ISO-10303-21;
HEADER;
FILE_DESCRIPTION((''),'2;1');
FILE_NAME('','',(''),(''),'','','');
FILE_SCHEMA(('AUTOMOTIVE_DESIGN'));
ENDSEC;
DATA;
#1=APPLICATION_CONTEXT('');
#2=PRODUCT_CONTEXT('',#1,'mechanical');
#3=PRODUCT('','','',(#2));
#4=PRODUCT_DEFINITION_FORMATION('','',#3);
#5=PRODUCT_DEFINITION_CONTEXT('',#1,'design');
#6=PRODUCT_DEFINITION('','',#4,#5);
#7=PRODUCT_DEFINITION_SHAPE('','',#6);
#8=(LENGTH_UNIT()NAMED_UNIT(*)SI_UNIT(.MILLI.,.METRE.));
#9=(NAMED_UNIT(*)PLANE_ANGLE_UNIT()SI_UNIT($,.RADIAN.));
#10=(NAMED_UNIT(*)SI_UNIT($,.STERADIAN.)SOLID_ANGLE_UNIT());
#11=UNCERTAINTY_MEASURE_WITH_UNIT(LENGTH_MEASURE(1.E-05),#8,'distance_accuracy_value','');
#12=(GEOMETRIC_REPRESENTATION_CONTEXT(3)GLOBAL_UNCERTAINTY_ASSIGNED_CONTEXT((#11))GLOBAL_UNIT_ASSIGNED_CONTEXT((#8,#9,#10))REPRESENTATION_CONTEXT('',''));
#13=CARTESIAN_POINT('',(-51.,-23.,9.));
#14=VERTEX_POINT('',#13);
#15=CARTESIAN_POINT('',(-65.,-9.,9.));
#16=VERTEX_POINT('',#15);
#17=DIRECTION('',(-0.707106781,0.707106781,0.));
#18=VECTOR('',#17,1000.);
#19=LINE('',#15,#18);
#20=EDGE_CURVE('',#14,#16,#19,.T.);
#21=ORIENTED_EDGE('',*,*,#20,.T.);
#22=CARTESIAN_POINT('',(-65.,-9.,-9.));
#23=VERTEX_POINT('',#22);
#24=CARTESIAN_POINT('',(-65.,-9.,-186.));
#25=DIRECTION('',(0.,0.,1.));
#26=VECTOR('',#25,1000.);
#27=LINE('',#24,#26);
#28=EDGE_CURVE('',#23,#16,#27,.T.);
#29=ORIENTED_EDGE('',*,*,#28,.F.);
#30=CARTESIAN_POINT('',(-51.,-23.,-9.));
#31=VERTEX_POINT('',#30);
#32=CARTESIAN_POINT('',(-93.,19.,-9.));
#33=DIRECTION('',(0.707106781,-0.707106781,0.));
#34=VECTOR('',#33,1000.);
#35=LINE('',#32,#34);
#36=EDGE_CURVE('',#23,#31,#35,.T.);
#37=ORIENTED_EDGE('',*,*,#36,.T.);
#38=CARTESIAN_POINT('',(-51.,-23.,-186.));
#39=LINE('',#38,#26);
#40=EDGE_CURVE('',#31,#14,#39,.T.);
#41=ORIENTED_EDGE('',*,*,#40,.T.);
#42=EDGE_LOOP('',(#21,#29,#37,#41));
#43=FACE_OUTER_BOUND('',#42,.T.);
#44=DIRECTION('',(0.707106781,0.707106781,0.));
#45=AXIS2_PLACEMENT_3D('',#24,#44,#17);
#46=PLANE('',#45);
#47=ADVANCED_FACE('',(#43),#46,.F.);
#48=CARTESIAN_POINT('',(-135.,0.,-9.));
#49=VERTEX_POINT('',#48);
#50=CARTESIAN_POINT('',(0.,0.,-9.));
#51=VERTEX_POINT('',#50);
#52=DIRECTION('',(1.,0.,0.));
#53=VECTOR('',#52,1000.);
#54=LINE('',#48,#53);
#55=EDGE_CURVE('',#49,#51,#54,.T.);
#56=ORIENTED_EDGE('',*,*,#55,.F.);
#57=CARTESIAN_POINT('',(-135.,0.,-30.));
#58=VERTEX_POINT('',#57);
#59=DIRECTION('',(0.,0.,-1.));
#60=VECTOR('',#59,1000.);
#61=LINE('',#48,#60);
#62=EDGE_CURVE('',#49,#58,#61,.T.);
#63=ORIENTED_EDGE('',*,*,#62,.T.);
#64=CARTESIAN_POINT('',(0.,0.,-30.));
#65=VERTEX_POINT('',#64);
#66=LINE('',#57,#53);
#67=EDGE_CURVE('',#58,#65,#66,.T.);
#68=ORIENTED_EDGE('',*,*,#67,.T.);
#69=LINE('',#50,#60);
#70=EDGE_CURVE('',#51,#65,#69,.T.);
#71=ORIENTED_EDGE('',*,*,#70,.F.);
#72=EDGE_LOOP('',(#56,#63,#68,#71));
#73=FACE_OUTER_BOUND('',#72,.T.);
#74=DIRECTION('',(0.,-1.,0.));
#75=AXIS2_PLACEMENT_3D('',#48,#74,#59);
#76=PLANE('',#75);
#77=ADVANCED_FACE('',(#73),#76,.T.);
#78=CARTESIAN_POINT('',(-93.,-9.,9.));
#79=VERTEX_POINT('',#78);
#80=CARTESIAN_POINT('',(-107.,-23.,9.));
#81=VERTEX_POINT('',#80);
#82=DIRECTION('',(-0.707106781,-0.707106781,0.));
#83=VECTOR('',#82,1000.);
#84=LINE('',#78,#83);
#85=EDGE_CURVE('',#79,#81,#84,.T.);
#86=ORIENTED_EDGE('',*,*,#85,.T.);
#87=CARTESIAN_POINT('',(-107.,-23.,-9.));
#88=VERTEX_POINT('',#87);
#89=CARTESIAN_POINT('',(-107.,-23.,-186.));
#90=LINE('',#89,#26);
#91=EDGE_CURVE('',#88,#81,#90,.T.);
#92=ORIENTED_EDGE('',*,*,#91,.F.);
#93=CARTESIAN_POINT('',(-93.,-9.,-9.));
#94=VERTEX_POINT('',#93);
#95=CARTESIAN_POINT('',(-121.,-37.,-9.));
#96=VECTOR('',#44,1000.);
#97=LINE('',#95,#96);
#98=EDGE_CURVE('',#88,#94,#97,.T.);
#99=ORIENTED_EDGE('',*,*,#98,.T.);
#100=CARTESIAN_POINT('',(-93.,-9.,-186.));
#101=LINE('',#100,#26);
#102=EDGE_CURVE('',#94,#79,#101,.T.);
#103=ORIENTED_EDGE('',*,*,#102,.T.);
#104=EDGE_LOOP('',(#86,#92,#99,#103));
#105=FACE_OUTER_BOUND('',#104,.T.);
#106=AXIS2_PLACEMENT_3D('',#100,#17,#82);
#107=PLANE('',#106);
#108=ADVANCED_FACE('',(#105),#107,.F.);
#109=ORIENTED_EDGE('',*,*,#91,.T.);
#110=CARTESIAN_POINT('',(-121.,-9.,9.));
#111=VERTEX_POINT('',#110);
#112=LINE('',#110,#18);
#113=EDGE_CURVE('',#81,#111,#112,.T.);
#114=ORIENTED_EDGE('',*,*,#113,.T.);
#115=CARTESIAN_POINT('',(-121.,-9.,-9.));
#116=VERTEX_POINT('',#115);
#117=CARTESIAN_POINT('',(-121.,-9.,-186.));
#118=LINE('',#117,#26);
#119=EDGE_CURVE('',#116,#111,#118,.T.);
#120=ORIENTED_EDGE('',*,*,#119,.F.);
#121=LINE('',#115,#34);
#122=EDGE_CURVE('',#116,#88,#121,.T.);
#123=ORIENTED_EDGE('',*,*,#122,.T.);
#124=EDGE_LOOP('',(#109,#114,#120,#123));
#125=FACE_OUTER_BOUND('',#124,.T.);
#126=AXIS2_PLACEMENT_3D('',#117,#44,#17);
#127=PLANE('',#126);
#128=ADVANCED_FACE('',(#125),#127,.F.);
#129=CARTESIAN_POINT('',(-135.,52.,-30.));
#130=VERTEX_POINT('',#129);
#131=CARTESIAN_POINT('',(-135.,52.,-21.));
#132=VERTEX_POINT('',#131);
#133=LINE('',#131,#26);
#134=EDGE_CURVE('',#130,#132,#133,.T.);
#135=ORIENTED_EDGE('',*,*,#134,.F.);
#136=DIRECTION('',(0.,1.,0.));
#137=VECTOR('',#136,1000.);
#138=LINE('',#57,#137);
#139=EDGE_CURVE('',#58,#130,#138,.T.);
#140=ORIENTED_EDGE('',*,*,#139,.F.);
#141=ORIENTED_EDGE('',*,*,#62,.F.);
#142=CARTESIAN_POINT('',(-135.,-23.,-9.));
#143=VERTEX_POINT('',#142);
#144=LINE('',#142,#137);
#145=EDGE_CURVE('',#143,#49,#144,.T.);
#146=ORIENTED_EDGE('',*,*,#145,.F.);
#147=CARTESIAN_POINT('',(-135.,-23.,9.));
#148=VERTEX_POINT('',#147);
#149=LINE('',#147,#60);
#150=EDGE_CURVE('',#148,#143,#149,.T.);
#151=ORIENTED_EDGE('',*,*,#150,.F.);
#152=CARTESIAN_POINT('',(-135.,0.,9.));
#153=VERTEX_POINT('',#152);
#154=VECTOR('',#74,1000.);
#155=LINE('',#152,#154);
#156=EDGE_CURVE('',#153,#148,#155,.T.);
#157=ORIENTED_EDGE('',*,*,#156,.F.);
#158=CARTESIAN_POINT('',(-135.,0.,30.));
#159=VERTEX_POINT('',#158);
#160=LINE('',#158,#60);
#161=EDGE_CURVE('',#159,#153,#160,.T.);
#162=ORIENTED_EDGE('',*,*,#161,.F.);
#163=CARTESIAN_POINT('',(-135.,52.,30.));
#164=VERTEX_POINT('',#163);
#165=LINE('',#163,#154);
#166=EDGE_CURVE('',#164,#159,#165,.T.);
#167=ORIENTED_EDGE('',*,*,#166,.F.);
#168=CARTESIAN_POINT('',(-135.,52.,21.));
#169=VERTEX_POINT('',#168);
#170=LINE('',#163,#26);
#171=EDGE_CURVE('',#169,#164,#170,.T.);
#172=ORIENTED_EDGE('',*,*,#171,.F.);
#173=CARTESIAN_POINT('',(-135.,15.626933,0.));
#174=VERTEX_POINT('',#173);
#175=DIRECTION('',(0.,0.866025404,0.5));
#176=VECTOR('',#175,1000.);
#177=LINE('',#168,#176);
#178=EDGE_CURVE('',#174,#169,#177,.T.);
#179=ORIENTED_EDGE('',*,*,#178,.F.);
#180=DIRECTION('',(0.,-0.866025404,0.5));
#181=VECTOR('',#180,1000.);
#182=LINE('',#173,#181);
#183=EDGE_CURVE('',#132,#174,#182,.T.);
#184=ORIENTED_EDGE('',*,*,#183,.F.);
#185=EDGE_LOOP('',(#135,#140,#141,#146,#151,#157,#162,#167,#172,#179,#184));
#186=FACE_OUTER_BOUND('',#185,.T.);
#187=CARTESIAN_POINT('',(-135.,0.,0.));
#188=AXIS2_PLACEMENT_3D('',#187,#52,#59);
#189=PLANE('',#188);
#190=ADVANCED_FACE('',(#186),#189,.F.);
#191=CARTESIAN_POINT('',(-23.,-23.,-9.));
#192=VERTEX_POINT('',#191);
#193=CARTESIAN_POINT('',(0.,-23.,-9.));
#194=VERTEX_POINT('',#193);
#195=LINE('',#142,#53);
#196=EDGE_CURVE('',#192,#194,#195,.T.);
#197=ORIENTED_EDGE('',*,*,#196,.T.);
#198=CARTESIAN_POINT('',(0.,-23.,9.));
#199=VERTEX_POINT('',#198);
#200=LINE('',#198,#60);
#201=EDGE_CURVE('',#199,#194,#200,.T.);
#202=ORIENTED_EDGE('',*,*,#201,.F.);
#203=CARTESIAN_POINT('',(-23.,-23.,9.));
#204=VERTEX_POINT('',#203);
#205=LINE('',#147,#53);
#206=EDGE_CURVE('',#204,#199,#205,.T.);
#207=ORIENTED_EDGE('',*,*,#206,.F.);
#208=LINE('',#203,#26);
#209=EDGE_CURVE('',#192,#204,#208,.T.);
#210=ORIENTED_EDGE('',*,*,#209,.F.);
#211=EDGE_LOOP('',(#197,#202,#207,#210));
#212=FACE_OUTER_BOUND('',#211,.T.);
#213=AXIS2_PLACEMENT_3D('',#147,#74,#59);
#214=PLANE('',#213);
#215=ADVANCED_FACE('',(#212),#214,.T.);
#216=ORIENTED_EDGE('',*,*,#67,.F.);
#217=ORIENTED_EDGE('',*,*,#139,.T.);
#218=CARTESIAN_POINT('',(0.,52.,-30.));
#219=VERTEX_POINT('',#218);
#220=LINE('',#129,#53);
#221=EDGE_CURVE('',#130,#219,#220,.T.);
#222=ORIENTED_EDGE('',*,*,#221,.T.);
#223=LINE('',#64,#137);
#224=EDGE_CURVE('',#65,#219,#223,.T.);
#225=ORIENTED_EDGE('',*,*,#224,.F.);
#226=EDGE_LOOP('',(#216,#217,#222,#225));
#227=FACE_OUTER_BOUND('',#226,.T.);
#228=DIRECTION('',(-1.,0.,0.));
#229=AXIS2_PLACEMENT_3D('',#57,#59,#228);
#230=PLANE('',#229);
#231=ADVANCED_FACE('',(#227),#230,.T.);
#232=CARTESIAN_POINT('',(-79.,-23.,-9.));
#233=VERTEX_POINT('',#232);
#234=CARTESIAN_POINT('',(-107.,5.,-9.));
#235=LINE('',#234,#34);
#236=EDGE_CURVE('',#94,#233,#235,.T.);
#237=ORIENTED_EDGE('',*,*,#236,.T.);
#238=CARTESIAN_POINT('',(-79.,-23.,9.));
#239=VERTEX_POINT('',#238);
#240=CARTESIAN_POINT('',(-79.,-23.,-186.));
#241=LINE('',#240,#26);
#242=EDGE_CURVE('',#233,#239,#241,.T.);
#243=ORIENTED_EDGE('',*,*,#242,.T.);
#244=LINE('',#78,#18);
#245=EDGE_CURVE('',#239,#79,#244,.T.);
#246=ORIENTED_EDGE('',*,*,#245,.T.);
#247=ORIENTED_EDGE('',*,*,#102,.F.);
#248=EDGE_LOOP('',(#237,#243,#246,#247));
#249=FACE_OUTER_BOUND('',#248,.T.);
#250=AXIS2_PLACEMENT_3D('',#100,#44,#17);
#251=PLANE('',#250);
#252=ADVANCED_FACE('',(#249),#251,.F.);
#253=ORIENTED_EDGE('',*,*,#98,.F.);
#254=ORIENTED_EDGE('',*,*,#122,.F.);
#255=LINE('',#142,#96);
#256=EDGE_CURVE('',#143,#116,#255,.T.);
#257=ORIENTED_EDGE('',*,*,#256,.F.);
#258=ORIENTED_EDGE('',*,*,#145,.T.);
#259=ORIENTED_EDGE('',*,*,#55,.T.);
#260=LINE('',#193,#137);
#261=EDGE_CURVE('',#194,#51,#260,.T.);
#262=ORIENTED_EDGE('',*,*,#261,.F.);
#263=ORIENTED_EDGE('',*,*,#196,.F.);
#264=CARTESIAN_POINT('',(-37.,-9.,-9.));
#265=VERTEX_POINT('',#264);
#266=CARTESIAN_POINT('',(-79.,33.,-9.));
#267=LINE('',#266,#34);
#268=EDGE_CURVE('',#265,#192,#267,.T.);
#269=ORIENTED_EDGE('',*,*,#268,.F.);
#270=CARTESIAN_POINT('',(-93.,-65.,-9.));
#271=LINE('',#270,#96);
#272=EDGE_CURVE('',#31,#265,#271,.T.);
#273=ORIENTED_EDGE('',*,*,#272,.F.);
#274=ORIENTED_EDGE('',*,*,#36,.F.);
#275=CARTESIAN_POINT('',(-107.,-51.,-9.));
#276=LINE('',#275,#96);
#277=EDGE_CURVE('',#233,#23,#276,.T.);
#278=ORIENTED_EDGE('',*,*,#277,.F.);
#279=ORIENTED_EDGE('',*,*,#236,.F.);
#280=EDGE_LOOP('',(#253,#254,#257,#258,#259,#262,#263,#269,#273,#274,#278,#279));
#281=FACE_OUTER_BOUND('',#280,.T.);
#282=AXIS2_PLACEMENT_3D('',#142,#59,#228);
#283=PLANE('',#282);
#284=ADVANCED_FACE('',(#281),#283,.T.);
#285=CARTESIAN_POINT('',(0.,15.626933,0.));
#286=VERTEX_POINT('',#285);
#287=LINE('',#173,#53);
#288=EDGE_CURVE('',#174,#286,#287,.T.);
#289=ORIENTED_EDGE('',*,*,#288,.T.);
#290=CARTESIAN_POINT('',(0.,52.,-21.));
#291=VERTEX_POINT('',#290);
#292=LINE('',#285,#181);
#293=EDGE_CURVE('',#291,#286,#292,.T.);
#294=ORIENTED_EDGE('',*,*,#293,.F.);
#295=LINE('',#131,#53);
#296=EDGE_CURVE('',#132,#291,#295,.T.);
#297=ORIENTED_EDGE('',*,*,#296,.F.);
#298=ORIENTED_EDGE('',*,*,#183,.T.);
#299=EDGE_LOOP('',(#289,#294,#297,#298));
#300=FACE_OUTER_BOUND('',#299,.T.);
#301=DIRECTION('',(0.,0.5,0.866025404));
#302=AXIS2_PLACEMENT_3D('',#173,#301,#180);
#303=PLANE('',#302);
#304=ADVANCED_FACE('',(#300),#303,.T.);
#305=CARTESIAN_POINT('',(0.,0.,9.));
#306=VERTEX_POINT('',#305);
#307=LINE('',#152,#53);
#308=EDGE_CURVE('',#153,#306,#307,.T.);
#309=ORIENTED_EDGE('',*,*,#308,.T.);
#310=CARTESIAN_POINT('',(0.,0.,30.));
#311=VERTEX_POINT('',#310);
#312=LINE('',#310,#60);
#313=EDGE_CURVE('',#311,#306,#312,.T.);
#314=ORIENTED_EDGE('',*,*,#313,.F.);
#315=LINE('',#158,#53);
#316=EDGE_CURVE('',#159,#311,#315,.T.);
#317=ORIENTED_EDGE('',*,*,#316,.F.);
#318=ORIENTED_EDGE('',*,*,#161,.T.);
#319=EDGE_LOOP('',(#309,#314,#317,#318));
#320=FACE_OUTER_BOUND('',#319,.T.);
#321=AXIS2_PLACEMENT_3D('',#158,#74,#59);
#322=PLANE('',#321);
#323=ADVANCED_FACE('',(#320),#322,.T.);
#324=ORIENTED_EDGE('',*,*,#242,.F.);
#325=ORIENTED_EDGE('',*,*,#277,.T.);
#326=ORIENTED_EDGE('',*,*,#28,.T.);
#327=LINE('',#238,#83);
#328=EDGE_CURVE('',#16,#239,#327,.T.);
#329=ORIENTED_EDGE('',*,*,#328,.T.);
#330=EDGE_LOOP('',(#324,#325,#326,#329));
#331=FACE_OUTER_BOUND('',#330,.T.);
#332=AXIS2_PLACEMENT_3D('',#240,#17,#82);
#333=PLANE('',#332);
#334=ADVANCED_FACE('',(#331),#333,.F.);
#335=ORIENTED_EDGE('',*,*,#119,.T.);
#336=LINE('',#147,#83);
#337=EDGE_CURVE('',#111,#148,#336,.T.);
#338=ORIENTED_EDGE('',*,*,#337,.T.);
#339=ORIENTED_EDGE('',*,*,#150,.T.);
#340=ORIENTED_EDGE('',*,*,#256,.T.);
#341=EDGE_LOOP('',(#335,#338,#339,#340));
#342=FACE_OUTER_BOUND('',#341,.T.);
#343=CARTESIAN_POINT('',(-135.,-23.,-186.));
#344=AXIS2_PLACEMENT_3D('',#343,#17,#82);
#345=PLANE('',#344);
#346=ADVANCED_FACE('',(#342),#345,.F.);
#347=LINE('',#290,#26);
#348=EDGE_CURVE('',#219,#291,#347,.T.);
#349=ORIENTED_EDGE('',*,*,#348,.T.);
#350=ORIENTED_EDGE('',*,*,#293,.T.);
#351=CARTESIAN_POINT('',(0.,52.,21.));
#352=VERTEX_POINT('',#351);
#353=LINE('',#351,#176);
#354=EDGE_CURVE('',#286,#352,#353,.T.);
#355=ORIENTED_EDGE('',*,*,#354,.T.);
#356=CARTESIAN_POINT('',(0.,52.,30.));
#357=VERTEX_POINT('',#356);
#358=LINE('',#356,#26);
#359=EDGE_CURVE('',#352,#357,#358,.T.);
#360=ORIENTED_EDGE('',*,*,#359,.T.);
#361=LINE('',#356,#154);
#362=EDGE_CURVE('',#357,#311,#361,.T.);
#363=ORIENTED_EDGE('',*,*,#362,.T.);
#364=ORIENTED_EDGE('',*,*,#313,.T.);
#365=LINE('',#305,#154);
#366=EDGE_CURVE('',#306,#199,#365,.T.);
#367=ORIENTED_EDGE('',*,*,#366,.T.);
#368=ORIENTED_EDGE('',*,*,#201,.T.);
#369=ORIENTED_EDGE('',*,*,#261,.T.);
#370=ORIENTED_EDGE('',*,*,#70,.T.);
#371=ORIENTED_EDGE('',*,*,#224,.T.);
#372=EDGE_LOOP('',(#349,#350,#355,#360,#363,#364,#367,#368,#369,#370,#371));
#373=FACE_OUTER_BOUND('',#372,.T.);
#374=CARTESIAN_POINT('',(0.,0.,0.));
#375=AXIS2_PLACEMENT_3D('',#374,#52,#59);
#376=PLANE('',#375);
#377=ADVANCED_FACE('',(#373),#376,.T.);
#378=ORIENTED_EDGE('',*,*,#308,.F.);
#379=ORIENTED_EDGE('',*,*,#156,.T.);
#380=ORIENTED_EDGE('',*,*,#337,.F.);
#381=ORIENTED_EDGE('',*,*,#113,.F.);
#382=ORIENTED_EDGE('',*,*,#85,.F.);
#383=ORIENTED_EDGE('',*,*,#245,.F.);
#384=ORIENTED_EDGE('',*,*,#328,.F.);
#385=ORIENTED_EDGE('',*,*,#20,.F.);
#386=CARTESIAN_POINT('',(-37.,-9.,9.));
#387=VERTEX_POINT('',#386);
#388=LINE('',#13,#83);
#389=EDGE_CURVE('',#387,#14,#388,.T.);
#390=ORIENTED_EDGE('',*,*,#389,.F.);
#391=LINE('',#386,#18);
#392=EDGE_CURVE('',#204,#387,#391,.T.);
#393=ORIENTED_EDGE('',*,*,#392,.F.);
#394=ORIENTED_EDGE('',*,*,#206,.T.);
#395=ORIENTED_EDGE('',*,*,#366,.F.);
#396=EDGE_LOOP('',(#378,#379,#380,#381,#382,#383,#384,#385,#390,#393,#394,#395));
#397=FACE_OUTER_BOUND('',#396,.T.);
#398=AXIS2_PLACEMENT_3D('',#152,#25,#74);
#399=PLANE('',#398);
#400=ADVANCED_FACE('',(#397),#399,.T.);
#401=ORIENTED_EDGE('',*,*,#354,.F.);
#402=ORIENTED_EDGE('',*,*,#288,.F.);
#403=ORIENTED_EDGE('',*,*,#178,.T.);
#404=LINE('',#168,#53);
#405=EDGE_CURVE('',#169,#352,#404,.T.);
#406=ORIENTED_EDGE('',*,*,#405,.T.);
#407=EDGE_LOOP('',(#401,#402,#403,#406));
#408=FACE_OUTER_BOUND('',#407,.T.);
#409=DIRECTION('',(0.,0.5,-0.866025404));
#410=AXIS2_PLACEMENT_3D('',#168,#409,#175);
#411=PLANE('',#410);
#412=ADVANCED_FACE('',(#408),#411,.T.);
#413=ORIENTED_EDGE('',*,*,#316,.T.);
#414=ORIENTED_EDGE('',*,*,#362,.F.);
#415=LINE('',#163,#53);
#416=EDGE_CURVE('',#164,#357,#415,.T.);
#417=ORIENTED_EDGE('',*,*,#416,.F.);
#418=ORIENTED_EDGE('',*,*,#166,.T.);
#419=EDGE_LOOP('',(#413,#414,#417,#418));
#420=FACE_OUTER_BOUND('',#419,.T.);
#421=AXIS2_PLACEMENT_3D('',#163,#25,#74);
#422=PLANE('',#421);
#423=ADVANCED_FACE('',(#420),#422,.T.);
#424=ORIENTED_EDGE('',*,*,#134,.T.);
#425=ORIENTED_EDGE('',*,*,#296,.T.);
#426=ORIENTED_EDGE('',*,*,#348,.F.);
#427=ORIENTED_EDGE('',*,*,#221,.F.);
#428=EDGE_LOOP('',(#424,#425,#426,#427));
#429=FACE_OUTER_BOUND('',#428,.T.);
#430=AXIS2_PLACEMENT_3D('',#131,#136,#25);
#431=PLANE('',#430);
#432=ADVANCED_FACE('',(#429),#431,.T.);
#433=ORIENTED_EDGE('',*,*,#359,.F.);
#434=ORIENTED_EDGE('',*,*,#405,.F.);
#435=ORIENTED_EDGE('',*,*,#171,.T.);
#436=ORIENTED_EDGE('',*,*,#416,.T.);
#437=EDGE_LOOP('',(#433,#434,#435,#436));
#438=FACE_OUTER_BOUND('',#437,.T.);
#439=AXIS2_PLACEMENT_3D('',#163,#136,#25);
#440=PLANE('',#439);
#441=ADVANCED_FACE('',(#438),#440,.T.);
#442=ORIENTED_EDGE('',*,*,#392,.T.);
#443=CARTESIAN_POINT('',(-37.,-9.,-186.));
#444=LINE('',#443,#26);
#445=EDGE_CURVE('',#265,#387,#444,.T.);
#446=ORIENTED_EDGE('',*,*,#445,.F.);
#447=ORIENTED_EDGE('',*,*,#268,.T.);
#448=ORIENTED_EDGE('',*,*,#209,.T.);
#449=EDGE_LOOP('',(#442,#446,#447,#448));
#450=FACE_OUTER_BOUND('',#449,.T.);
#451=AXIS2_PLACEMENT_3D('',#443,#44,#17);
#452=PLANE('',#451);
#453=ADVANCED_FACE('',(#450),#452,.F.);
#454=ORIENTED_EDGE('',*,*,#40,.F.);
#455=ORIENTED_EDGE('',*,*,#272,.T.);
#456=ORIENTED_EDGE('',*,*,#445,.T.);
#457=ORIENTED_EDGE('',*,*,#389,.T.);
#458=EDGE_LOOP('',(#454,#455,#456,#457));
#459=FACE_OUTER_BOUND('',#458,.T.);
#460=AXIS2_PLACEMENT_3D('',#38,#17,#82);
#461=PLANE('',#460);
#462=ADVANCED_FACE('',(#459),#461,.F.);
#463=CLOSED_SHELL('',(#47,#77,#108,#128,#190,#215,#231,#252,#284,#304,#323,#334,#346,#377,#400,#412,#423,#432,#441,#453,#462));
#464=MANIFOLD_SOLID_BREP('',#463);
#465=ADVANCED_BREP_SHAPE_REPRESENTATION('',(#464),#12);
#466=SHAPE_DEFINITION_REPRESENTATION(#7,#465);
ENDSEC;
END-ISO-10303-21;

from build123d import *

# Parameters (mm, degrees)
V_BLOCK_BODY_DEPTH          = 135
UNDERSIDE_NOTCHES_CUT_DEPTH = 195


with BuildPart() as part:
    # V-Block Profile Sketch → V-Block Body (new body)
    with BuildSketch(Plane(origin=(0, 0, 0), x_dir=(0, 0, -1), z_dir=(1, 0, 0))):
        Polygon((-30, 52), (-30, 0), (-9, 0), (-9, -23), (9, -23), (9, 0), (30, 0), (30, 52), (21, 52), (0, 15.626933041), (-21, 52), align=None)
    extrude(amount=-V_BLOCK_BODY_DEPTH)

    # Underside Notches Sketch → Underside Notches Cut (cut)
    with BuildSketch(Plane.XY.offset(9)):
        Polygon((-135, -23), (-121, -9), (-107, -23), (-93, -9), (-79, -23), (-65, -9), (-51, -23), (-37, -9), (-7.657800388, -38.342199612), (-135, -44.429564146), align=None)
    extrude(amount=-UNDERSIDE_NOTCHES_CUT_DEPTH, mode=Mode.SUBTRACT)


solid = part.part
